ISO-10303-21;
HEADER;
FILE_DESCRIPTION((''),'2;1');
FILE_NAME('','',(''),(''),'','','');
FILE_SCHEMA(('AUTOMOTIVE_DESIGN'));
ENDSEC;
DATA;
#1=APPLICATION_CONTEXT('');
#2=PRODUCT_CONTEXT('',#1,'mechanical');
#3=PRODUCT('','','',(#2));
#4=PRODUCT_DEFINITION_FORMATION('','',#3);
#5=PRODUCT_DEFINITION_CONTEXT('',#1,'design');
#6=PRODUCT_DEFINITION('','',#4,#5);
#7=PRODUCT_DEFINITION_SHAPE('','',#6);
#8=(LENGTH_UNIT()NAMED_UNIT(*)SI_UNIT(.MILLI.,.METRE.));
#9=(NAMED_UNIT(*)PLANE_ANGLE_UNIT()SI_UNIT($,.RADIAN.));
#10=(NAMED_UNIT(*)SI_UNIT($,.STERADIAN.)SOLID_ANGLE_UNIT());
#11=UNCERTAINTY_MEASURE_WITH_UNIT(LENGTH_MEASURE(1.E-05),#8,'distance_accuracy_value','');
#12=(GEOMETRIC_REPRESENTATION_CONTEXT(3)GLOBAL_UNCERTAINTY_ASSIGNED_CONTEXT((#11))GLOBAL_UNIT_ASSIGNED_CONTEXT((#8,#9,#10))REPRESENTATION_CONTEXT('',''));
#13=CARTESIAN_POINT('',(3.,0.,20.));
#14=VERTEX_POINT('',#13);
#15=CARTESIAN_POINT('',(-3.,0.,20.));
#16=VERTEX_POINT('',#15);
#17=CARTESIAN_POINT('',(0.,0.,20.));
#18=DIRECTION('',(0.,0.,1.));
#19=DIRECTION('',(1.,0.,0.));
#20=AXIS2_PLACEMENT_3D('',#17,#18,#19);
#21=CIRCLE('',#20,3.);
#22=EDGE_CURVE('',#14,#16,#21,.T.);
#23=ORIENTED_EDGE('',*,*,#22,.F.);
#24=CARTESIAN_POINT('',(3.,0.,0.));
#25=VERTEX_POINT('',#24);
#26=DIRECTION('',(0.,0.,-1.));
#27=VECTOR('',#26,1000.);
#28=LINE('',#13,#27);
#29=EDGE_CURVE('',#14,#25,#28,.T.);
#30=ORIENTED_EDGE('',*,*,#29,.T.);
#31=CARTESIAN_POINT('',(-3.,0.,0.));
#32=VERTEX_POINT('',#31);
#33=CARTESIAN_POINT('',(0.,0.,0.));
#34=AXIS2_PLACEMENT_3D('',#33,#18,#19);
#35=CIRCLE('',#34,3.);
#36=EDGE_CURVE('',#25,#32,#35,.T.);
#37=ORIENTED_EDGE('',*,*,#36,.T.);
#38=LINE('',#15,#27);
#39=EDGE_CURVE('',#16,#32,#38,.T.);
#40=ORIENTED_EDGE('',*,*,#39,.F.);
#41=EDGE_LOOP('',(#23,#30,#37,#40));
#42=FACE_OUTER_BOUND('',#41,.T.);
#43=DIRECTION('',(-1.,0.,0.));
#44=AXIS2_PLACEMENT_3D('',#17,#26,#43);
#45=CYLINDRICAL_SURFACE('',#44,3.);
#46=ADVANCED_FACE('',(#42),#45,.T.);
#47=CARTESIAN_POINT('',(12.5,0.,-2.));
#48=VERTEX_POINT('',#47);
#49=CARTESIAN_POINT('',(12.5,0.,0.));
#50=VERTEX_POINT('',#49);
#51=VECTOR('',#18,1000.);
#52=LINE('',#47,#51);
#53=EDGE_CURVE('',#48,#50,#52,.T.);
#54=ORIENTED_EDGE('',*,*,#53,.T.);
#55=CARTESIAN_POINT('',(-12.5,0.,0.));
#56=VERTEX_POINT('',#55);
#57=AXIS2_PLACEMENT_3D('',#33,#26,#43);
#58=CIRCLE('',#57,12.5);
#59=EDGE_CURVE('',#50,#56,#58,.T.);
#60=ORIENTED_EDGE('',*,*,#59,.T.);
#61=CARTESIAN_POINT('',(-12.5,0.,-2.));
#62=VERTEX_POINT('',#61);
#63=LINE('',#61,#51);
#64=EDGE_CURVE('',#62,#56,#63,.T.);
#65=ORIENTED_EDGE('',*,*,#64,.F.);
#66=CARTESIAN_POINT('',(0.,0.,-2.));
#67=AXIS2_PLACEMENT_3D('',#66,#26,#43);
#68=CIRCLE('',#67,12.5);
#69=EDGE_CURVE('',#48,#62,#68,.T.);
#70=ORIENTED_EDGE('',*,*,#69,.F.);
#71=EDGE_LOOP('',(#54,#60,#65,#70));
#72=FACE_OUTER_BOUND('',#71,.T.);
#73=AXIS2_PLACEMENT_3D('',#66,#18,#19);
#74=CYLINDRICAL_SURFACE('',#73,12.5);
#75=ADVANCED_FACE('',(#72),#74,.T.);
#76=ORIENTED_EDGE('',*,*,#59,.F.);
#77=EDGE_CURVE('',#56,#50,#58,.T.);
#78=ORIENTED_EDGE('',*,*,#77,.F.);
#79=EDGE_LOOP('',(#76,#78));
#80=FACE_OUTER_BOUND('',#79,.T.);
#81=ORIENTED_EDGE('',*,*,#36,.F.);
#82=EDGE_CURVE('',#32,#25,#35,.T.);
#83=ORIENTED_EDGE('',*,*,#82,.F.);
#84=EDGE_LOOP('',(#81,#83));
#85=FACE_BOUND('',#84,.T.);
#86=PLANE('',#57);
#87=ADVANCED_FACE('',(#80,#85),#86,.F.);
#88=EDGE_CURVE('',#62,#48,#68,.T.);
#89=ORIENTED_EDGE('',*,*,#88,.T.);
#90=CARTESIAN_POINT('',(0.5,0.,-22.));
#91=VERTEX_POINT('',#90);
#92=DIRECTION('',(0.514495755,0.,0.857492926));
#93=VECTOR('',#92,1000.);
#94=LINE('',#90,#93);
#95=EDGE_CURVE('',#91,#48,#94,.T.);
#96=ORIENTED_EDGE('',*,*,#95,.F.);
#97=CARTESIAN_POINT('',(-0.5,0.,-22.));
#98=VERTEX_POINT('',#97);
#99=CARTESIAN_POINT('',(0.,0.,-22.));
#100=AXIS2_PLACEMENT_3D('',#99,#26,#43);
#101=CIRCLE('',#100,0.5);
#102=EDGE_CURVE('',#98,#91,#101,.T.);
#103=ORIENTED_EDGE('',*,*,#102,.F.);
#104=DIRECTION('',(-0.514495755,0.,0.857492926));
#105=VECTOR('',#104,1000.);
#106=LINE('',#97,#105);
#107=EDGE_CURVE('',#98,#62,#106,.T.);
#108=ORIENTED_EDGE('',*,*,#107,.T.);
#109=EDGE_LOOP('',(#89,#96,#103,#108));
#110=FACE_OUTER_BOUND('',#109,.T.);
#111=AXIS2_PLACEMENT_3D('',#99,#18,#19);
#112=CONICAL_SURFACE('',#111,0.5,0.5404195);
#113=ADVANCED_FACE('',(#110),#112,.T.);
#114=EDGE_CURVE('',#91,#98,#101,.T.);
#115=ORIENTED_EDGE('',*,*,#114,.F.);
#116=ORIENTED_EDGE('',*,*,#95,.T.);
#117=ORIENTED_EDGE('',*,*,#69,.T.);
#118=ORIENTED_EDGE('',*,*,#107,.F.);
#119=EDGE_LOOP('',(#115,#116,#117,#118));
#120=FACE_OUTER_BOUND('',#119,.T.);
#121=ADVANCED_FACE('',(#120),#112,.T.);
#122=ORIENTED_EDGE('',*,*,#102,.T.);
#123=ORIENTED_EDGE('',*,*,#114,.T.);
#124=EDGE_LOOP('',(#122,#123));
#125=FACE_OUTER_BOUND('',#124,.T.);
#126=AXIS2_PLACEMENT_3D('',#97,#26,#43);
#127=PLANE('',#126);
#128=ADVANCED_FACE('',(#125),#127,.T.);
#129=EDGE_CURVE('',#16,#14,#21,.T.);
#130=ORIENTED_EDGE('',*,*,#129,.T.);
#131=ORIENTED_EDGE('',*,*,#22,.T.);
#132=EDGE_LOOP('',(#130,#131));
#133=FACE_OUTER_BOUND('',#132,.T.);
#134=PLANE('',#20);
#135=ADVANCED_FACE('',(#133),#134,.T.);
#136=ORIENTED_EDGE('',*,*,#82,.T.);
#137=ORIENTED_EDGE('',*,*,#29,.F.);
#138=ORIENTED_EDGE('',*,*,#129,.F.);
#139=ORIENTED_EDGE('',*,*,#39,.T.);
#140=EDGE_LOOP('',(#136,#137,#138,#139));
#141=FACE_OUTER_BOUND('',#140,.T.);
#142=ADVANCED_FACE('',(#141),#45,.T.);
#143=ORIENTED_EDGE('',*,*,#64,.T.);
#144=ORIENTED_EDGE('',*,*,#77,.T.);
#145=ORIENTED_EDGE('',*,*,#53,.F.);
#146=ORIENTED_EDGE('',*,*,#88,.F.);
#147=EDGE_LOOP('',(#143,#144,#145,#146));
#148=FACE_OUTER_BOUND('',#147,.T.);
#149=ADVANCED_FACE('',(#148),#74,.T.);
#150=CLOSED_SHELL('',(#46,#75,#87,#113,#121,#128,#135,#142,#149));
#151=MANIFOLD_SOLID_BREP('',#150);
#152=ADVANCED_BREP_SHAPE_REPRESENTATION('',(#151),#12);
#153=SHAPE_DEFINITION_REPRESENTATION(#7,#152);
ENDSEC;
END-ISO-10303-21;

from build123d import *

# Parameters (mm, degrees)
SKETCH1_R           = 3
BOSS_EXTRUDE1_DEPTH = 20
SKETCH2_R           = 12.5
BOSS_EXTRUDE2_DEPTH = 2


with BuildPart() as part:
    # Sketch1 → Boss-Extrude1 (new body)
    with BuildSketch(Plane.XY):
        Circle(SKETCH1_R)
    extrude(amount=BOSS_EXTRUDE1_DEPTH)

    # Sketch2 → Boss-Extrude2 (add)
    with BuildSketch(Plane(origin=(0, 0, 0), x_dir=(-1, 0, 0), z_dir=(0, 0, -1))):
        Circle(SKETCH2_R)
    extrude(amount=BOSS_EXTRUDE2_DEPTH)

    # Sketch3 → Revolve2 (revolve)
    with BuildSketch(Plane(origin=(0, 0, 0), x_dir=(1, 0, 0), z_dir=(0, 1, 0)), mode=Mode.PRIVATE) as revolve2_sk:
        Polygon((-12.5, 2), (-0.5, 22), (0, 22), (0, 2), align=None)
    revolve(revolve2_sk.sketch.rotate(Axis((0, 0, -22), (0, 0, 1)), 180), axis=Axis((0, 0, -22), (0, 0, 1)))


solid = part.part
